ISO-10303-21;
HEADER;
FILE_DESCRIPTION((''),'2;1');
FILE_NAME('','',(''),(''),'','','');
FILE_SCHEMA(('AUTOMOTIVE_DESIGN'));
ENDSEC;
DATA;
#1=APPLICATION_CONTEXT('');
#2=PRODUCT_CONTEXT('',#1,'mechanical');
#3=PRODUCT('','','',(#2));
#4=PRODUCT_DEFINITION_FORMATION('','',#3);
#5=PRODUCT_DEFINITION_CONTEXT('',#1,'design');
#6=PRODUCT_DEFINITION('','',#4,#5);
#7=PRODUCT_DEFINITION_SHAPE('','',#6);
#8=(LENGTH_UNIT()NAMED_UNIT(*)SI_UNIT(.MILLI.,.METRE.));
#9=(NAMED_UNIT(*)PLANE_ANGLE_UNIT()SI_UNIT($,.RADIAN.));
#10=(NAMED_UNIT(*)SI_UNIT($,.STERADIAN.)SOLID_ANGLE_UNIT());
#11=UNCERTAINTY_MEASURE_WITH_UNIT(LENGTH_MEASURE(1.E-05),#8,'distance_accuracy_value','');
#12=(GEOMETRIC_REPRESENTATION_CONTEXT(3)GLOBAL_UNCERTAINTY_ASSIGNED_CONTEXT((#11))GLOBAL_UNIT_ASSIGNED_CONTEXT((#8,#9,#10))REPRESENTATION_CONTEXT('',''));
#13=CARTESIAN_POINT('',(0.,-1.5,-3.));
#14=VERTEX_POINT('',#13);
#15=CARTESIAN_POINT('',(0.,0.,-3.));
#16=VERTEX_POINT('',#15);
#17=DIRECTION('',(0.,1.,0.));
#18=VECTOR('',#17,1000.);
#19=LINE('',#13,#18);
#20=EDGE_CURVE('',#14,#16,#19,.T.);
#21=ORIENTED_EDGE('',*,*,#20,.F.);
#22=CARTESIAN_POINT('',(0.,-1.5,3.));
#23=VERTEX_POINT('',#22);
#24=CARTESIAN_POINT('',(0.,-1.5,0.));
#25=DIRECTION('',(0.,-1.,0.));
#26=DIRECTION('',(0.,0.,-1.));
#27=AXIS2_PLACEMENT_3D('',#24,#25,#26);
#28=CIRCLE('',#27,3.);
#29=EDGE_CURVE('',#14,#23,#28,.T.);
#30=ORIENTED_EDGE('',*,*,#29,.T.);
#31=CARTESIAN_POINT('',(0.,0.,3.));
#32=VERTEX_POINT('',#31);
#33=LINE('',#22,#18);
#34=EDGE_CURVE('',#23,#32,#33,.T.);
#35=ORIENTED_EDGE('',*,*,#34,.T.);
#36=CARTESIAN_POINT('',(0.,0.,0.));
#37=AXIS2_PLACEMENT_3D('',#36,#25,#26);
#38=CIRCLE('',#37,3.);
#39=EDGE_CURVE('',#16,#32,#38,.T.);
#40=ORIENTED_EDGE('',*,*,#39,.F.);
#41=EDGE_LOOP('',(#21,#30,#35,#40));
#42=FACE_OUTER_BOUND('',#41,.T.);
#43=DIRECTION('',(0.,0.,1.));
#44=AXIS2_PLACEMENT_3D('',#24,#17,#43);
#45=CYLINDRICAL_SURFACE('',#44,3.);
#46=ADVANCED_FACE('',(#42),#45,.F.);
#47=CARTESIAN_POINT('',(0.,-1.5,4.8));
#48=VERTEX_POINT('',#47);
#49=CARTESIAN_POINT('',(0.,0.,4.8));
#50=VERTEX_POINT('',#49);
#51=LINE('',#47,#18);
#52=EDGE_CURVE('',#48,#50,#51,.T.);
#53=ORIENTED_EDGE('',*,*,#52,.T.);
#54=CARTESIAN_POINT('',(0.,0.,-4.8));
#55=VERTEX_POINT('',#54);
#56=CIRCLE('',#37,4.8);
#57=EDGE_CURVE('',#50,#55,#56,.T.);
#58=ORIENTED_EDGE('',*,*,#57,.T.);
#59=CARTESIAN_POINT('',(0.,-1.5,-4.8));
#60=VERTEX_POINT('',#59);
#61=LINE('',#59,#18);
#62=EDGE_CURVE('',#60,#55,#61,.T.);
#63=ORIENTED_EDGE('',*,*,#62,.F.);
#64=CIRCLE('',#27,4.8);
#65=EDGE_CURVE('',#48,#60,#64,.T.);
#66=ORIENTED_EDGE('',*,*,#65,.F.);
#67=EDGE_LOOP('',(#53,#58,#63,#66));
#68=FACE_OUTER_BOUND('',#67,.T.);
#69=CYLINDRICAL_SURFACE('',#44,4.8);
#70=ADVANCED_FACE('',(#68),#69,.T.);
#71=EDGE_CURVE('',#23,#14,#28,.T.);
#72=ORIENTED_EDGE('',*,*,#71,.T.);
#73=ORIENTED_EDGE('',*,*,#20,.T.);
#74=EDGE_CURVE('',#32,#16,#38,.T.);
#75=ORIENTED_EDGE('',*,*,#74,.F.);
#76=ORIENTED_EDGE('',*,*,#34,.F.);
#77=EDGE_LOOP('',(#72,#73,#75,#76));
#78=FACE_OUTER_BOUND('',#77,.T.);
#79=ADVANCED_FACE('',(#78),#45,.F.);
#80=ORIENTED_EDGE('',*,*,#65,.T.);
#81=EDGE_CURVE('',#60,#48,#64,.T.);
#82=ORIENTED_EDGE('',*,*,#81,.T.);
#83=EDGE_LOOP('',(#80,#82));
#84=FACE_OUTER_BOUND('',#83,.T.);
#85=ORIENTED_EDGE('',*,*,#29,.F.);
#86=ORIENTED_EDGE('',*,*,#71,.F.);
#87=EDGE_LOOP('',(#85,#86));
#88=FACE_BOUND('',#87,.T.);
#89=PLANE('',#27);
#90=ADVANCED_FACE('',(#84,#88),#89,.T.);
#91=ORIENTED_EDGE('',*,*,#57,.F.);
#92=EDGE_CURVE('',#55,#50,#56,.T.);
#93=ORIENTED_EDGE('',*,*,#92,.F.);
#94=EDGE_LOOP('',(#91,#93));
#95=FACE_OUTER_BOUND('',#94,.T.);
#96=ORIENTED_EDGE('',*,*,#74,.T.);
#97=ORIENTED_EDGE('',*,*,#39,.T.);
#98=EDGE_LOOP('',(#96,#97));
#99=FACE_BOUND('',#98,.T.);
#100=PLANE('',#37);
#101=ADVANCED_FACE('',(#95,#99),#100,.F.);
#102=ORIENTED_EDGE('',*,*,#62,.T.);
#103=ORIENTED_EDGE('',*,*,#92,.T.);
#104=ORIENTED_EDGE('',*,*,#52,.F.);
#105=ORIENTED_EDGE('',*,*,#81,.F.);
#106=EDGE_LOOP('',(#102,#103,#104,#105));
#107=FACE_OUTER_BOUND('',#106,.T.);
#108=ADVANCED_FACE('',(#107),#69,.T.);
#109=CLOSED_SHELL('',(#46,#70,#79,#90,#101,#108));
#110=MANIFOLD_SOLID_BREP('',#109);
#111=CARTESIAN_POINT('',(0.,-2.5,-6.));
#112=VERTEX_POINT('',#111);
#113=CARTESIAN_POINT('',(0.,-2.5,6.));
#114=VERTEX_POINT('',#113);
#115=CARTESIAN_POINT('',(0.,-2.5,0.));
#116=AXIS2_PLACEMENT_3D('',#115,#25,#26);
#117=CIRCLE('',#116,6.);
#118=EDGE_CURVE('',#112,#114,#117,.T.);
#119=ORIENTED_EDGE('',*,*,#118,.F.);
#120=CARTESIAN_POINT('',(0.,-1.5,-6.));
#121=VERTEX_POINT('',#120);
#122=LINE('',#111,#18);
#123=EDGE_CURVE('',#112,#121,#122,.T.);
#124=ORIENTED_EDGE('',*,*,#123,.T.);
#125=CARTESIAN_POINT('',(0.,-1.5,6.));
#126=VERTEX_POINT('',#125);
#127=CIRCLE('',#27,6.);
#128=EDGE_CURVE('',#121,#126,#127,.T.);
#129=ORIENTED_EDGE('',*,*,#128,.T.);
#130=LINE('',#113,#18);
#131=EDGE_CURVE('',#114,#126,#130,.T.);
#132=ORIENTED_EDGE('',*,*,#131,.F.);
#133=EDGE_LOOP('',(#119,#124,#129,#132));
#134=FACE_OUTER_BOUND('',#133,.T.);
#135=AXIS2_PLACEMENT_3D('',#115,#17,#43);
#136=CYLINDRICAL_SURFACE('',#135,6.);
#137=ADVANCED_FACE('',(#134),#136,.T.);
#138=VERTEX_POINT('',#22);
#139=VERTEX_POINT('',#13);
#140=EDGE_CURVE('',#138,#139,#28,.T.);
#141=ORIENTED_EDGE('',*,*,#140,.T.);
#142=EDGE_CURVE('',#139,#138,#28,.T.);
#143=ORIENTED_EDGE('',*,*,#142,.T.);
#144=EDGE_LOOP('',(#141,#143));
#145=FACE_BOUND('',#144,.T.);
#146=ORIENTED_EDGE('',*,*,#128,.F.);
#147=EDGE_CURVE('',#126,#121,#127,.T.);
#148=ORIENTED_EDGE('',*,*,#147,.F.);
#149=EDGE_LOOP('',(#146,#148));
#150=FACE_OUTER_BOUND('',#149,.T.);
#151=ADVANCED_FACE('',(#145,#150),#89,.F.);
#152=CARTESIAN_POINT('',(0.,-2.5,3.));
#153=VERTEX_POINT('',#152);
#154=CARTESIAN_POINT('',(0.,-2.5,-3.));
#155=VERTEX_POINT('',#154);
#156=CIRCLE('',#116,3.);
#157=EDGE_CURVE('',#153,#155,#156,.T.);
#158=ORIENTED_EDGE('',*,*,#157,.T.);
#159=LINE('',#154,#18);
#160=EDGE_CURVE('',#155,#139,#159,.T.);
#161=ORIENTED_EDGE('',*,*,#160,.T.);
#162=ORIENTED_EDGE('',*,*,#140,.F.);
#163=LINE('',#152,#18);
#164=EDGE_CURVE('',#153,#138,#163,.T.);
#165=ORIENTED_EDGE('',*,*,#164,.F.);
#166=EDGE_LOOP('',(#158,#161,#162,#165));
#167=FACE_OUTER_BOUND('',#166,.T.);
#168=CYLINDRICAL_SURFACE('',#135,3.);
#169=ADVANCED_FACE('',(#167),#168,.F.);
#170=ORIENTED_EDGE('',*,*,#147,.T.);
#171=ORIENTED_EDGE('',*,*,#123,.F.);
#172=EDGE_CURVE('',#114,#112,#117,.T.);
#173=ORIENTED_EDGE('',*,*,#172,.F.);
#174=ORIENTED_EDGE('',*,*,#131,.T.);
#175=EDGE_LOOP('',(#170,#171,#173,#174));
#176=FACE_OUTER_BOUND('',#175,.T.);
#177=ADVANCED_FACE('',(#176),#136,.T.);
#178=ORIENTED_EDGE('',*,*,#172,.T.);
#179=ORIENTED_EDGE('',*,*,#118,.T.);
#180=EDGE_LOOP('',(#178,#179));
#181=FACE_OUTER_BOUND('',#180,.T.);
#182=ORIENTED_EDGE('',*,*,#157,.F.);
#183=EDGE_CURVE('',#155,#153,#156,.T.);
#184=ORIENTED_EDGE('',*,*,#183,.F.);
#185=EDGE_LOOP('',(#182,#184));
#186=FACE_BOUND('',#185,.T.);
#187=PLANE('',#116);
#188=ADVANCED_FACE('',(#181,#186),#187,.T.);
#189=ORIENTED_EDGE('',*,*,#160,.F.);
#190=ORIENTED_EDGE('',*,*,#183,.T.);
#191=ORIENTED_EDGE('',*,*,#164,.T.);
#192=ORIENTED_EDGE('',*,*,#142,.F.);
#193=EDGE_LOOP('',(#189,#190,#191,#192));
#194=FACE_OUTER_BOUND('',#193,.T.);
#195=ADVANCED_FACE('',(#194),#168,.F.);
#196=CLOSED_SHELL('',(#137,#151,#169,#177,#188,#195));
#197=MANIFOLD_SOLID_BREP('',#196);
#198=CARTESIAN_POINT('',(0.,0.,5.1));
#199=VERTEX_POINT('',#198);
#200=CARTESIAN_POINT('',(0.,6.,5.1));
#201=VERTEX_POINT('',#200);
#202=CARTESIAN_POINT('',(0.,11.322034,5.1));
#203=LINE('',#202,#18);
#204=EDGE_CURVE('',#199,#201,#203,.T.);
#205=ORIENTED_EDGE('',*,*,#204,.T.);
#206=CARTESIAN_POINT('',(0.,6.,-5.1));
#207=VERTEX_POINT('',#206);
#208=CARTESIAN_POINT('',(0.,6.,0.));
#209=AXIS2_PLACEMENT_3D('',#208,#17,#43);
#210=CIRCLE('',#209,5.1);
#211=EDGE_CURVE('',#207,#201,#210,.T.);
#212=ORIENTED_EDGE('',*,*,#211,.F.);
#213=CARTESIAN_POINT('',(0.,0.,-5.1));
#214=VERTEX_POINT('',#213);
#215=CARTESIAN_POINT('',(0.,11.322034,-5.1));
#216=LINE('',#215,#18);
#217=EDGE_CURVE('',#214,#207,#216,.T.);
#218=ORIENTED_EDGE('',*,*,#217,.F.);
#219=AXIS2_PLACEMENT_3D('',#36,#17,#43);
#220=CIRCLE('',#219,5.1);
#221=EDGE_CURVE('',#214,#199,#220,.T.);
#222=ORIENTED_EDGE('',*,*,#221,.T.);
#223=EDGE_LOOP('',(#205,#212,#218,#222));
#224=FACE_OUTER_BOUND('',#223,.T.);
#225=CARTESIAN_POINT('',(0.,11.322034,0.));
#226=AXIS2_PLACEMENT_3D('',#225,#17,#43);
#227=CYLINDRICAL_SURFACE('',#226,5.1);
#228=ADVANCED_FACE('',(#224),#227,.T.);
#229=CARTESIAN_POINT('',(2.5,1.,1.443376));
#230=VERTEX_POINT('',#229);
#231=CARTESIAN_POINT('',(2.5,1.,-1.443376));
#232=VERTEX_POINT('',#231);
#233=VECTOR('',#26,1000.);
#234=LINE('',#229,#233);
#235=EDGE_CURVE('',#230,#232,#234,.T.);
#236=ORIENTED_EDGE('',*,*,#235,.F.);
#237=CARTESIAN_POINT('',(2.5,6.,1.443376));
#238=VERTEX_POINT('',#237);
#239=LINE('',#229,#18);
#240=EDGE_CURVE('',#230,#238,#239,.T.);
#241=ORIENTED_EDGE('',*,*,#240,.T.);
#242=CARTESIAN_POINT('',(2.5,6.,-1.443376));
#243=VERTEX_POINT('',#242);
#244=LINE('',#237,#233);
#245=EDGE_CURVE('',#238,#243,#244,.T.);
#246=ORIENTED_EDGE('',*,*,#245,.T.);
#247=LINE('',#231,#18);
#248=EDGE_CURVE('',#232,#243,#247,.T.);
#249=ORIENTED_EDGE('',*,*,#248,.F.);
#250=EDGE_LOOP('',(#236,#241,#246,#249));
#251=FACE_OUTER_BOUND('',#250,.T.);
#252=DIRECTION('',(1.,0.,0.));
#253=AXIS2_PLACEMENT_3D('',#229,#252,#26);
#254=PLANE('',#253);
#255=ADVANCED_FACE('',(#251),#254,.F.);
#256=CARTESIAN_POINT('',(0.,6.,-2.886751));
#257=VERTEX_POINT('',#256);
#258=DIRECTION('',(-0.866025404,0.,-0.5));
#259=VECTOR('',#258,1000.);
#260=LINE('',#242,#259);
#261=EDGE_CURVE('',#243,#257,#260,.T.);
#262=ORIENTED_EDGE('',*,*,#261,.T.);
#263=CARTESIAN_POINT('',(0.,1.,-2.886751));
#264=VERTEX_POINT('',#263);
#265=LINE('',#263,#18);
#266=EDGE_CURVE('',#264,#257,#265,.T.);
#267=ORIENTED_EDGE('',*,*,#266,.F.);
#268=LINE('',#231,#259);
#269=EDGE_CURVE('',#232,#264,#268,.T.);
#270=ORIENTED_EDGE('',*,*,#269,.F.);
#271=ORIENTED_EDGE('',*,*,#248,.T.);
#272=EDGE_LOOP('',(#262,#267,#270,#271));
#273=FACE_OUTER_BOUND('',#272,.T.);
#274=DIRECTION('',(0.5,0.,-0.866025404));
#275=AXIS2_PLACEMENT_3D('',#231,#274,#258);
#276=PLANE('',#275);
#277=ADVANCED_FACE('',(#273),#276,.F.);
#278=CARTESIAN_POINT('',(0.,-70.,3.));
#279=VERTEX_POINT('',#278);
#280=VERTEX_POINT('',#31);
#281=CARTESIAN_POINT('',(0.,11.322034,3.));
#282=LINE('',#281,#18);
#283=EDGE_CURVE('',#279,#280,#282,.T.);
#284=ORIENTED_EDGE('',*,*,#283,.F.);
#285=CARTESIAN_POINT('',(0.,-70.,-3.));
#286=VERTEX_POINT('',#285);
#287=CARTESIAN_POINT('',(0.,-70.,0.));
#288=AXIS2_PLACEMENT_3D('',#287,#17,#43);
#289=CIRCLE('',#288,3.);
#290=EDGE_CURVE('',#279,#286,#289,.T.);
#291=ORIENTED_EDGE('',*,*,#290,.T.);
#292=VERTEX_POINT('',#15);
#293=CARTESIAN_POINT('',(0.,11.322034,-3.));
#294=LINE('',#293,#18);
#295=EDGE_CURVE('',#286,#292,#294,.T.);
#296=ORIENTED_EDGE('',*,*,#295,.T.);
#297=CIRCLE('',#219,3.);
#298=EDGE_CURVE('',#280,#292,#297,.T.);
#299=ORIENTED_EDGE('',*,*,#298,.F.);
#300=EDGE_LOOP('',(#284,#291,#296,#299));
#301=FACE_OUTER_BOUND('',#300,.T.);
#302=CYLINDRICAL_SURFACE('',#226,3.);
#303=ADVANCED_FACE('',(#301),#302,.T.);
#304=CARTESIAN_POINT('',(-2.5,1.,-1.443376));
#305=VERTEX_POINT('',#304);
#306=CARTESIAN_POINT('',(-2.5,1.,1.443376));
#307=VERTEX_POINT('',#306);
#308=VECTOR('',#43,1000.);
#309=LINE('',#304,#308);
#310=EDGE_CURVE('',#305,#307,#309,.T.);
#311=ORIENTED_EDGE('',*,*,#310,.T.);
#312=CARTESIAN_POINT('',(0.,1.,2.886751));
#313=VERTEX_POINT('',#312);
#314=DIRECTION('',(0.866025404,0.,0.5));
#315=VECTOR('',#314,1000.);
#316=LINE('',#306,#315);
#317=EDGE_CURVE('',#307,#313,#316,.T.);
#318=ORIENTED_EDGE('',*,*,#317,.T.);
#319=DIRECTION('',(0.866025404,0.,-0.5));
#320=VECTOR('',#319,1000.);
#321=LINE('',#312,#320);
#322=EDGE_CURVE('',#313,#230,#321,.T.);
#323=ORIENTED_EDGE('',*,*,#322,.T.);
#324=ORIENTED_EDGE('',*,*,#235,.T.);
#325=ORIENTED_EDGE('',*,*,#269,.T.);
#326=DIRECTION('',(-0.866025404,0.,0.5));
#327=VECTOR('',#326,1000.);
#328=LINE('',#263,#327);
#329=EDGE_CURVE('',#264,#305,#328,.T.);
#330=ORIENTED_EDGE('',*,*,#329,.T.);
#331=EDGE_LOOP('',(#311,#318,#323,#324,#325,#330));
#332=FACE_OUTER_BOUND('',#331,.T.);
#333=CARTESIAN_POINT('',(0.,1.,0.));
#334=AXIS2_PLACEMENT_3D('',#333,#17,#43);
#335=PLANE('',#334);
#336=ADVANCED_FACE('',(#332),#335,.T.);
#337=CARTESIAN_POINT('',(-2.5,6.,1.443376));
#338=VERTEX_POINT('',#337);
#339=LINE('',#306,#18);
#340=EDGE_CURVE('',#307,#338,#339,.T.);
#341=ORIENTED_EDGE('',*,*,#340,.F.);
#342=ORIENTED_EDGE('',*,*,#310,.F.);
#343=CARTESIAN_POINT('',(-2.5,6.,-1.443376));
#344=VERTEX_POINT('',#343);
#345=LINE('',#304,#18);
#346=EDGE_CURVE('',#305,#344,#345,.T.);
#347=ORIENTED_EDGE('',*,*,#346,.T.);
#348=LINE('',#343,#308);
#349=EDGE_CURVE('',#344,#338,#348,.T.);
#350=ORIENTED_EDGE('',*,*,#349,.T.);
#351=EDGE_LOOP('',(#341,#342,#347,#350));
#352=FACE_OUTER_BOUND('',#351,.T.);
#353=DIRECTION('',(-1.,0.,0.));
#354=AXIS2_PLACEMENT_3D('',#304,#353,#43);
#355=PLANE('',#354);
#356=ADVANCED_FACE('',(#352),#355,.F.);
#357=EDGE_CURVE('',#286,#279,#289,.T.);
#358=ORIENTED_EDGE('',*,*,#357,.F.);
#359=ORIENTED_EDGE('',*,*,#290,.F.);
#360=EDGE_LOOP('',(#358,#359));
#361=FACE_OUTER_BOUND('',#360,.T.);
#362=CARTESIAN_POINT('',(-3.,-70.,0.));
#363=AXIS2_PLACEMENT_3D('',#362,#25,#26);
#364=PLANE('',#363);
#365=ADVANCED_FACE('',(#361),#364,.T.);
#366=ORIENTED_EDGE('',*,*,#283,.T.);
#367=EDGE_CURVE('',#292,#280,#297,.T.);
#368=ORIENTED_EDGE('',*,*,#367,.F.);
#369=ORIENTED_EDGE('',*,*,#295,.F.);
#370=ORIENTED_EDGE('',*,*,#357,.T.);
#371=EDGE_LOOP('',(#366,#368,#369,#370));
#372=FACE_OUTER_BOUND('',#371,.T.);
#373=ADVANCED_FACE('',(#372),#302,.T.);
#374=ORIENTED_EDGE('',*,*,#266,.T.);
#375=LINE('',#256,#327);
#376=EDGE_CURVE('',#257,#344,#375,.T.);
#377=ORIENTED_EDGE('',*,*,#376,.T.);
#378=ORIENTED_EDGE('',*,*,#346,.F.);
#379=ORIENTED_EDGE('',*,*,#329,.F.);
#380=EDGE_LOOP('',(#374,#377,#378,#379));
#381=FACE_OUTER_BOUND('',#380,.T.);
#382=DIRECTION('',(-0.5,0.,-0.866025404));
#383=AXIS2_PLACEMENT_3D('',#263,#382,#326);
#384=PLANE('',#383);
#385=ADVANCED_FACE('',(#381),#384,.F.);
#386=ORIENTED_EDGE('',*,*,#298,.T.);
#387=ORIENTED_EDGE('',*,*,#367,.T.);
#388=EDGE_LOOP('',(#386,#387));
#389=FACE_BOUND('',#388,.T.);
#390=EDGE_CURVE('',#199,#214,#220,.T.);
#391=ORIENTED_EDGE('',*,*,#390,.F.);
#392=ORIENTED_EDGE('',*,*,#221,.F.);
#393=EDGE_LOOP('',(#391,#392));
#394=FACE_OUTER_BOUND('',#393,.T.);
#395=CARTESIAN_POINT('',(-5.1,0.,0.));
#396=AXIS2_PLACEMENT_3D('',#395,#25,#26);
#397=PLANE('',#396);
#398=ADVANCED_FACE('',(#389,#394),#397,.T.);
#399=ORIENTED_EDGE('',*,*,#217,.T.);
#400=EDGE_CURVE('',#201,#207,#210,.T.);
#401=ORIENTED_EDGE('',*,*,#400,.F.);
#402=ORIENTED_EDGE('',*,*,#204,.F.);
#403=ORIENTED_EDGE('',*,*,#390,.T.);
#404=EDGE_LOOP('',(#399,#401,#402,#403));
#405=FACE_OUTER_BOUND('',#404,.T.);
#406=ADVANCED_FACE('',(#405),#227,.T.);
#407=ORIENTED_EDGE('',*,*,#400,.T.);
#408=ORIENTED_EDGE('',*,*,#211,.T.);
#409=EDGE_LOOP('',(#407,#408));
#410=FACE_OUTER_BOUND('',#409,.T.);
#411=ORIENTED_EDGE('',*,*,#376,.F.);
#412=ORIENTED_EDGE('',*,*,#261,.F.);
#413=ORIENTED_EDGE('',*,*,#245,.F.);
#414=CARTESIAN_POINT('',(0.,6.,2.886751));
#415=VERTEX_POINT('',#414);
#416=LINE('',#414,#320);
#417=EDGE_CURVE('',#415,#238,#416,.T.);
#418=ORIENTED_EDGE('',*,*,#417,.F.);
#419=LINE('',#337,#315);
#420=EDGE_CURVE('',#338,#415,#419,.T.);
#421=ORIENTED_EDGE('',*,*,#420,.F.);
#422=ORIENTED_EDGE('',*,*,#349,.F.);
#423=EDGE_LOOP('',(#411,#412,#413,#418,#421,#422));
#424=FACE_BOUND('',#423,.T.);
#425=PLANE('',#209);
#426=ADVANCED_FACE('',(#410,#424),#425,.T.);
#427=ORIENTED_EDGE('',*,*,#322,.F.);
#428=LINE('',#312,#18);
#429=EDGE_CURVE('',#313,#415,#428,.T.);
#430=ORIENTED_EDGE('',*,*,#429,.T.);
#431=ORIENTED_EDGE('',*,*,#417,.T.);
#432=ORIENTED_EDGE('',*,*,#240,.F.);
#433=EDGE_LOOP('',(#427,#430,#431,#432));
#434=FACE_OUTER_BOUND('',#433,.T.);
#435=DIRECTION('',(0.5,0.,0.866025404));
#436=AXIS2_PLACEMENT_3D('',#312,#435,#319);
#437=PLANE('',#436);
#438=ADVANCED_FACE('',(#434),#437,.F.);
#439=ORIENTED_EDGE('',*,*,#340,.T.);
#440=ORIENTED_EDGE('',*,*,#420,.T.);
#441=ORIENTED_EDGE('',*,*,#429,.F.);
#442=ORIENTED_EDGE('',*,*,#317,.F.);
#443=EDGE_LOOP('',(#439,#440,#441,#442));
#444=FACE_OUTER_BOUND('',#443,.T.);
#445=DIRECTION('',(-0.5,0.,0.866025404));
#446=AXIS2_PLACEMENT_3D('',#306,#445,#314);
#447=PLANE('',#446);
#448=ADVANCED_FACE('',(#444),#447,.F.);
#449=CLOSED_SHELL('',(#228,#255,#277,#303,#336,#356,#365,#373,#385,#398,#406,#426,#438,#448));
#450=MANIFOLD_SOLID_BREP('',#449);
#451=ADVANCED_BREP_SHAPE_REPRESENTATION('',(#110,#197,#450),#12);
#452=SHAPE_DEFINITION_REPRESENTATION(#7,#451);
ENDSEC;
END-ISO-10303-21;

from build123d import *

# Parameters (mm, degrees)
CUT_EXTRUDE_1_DEPTH  = 5
SKETCH_3_R           = 4.8
SKETCH_3_R_2         = 3
BOSS_EXTRUDE_1_DEPTH = 1.5
SKETCH_4_R           = 6
SKETCH_4_R_2         = 3
BOSS_EXTRUDE_2_DEPTH = 1


with BuildPart() as part:
    # Sketch 1 → Revolve 1 (revolve)
    with BuildSketch(Plane.XY, mode=Mode.PRIVATE) as revolve_1_sk:
        Polygon((0, 6), (-5.1, 6), (-5.1, 0), (-3, 0), (-3, -70), (0, -70), align=None)
    revolve(revolve_1_sk.sketch.rotate(Axis((0, 11.322033898, 0), (0, -1, 0)), 270), axis=Axis((0, 11.322033898, 0), (0, -1, 0)))

    # Sketch 2 → Cut-Extrude 1 (cut)
    with BuildSketch(Plane(origin=(0, 6, 0), x_dir=(1, 0, 0), z_dir=(0, 1, 0))):
        Polygon((0, 2.886751346), (-2.5, 1.443375673), (-2.5, -1.443375673), (0, -2.886751346), (2.5, -1.443375673), (2.5, 1.443375673), align=None)
    extrude(amount=-CUT_EXTRUDE_1_DEPTH, mode=Mode.SUBTRACT)


with BuildPart() as body_2:
    # Sketch 3 → Boss-Extrude 1 (new body)
    with BuildSketch(Plane.XZ):
        with Locations(Location((0, 0, 0), (0, 0, 270))):
            Circle(SKETCH_3_R)
        with Locations(Location((0, 0, 0), (0, 0, 270))):
            Circle(SKETCH_3_R_2, mode=Mode.SUBTRACT)
    extrude(amount=BOSS_EXTRUDE_1_DEPTH)


with BuildPart() as body_3:
    # Sketch 4 → Boss-Extrude 2 (new body)
    with BuildSketch(Plane.XZ.offset(1.5)):
        with Locations(Location((0, 0, 0), (0, 0, 270))):
            Circle(SKETCH_4_R)
        with Locations(Location((0, 0, 0), (0, 0, 270))):
            Circle(SKETCH_4_R_2, mode=Mode.SUBTRACT)
    extrude(amount=BOSS_EXTRUDE_2_DEPTH)


solid = Compound([part.part, body_2.part, body_3.part])
